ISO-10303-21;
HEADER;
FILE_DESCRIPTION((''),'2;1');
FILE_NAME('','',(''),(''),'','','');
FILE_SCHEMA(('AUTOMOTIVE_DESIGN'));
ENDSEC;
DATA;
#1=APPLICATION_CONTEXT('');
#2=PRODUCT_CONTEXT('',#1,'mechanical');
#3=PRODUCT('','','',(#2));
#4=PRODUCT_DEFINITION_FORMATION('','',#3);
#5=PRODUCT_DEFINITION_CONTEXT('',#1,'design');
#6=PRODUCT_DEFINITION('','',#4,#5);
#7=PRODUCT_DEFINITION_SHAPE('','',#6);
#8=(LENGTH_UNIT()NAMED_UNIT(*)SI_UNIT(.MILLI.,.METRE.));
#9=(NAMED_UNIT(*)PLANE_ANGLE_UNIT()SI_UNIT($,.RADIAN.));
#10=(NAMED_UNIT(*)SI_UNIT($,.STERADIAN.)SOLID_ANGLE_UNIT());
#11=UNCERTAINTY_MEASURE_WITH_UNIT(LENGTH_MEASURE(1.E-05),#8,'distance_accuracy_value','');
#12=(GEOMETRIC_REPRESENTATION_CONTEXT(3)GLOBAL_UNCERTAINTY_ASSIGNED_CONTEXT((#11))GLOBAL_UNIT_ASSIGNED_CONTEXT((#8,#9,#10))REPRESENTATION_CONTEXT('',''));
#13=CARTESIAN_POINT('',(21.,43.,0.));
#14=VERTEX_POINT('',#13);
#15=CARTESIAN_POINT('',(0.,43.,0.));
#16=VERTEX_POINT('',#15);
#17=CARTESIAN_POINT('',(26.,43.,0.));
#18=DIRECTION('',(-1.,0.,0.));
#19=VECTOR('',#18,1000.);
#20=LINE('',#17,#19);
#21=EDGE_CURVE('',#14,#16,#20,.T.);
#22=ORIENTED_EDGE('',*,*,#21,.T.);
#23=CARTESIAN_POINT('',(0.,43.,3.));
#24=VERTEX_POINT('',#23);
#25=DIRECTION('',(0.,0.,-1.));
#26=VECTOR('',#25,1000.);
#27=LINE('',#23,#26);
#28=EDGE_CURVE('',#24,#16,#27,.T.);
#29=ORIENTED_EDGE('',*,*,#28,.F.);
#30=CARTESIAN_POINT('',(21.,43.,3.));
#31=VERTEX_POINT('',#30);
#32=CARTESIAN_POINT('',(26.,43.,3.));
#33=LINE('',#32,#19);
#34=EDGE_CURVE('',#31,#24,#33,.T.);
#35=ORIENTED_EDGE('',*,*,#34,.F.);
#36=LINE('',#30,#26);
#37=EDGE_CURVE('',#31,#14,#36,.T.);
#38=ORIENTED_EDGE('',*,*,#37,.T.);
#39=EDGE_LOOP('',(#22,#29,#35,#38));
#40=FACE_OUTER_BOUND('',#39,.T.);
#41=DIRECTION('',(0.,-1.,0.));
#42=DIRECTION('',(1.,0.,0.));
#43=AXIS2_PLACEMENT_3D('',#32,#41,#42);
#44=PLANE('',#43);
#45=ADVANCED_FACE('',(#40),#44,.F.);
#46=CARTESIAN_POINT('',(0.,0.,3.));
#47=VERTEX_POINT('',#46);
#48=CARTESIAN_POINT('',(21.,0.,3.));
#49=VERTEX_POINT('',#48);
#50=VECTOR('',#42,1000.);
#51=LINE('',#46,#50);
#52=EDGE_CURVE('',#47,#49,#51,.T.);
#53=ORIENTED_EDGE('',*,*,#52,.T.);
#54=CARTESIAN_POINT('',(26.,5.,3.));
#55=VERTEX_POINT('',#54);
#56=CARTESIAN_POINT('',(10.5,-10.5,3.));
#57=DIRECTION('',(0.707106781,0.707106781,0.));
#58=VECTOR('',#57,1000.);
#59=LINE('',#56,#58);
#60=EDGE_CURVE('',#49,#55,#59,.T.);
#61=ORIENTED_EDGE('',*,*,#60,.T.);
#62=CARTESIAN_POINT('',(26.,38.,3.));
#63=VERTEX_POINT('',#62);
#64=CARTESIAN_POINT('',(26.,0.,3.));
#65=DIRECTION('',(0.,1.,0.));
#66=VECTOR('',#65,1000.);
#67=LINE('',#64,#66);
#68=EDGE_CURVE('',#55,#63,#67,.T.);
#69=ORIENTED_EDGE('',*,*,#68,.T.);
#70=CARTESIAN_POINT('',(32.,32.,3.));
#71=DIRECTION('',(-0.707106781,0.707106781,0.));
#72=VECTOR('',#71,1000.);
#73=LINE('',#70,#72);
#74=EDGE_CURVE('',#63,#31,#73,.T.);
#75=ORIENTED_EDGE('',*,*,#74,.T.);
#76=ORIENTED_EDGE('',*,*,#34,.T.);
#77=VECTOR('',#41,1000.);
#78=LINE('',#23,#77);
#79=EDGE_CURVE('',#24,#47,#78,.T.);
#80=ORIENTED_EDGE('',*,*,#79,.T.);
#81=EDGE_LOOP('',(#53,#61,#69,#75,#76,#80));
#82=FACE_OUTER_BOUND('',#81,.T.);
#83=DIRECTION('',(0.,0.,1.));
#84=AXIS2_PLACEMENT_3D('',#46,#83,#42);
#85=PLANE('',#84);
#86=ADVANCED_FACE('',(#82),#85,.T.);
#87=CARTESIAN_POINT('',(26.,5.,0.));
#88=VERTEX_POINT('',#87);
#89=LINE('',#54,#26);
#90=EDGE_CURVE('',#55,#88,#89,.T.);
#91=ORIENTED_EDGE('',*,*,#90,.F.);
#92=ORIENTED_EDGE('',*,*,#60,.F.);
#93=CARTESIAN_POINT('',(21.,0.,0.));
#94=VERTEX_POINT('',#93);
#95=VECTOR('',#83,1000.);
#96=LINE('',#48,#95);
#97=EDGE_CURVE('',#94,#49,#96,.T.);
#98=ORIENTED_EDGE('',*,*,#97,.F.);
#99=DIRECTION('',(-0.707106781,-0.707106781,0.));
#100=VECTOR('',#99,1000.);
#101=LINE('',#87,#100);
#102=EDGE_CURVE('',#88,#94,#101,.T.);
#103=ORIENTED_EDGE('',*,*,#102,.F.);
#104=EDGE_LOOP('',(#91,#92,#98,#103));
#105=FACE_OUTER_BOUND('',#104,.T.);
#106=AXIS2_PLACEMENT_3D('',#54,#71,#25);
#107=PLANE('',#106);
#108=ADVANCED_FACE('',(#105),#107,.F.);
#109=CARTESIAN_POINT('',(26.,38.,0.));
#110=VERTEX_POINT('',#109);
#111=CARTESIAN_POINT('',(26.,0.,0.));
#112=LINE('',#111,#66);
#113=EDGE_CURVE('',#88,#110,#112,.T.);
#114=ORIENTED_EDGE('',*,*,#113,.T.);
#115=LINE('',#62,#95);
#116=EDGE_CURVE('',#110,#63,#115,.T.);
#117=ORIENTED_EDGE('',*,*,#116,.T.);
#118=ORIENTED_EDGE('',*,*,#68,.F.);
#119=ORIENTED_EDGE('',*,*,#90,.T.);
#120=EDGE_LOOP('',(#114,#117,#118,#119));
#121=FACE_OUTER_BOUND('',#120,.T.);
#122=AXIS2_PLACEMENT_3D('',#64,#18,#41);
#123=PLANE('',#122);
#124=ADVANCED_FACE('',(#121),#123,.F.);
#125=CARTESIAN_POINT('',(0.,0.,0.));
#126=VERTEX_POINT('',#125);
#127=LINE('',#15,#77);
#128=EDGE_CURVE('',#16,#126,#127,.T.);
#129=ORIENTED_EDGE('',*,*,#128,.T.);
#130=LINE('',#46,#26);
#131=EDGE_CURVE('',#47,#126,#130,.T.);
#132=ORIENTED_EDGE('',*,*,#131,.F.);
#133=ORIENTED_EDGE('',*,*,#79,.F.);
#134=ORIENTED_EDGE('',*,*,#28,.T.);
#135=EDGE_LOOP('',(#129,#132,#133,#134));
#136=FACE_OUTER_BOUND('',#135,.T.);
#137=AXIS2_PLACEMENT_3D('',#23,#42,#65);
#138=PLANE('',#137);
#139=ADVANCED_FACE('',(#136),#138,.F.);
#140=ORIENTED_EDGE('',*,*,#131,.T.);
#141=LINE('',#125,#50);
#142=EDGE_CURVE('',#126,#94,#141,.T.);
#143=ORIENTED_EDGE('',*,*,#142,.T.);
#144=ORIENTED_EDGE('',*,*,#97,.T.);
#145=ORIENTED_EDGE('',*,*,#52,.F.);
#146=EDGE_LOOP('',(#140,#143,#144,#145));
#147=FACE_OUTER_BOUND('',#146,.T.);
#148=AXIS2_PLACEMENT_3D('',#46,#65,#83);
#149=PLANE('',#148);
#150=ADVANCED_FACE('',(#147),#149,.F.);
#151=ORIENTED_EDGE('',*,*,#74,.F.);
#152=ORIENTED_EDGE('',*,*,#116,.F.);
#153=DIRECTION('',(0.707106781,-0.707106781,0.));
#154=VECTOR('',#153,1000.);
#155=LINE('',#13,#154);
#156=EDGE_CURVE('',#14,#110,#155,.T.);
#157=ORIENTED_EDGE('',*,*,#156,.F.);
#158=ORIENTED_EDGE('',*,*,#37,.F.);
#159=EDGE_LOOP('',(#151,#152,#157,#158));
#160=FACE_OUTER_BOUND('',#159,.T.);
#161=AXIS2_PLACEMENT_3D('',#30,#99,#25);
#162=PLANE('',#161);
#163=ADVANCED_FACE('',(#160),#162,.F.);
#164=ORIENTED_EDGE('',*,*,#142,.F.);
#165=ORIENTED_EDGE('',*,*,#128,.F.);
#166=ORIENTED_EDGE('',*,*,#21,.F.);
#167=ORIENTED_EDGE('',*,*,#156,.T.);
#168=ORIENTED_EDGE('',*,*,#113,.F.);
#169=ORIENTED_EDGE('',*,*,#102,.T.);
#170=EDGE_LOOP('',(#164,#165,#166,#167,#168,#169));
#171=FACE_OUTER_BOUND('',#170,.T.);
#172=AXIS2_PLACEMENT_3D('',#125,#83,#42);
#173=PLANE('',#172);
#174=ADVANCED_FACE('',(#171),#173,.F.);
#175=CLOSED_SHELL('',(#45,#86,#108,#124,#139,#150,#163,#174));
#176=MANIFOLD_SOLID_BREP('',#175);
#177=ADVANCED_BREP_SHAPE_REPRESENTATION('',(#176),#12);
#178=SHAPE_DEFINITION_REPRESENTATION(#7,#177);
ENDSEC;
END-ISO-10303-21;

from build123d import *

# Parameters (mm, degrees)
SKETCH_1_W      = 26
SKETCH_1_H      = 43
EXTRUDE_1_DEPTH = 3
CHAMFER_1_SIZE  = 5


with BuildPart() as part:
    # 草图1 → 凸台-拉伸1 (new body)
    with BuildSketch(Plane.XY):
        with Locations((13, 21.5)):
            Rectangle(SKETCH_1_W, SKETCH_1_H)
    extrude(amount=EXTRUDE_1_DEPTH)

    # 倒角1
    chamfer_1_edges = [part.edges().sort_by_distance(p)[0] for p in [
        (26, 43, 1.5),
        (26, 0, 1.5),
    ]]
    chamfer(chamfer_1_edges, length=CHAMFER_1_SIZE)


solid = part.part
